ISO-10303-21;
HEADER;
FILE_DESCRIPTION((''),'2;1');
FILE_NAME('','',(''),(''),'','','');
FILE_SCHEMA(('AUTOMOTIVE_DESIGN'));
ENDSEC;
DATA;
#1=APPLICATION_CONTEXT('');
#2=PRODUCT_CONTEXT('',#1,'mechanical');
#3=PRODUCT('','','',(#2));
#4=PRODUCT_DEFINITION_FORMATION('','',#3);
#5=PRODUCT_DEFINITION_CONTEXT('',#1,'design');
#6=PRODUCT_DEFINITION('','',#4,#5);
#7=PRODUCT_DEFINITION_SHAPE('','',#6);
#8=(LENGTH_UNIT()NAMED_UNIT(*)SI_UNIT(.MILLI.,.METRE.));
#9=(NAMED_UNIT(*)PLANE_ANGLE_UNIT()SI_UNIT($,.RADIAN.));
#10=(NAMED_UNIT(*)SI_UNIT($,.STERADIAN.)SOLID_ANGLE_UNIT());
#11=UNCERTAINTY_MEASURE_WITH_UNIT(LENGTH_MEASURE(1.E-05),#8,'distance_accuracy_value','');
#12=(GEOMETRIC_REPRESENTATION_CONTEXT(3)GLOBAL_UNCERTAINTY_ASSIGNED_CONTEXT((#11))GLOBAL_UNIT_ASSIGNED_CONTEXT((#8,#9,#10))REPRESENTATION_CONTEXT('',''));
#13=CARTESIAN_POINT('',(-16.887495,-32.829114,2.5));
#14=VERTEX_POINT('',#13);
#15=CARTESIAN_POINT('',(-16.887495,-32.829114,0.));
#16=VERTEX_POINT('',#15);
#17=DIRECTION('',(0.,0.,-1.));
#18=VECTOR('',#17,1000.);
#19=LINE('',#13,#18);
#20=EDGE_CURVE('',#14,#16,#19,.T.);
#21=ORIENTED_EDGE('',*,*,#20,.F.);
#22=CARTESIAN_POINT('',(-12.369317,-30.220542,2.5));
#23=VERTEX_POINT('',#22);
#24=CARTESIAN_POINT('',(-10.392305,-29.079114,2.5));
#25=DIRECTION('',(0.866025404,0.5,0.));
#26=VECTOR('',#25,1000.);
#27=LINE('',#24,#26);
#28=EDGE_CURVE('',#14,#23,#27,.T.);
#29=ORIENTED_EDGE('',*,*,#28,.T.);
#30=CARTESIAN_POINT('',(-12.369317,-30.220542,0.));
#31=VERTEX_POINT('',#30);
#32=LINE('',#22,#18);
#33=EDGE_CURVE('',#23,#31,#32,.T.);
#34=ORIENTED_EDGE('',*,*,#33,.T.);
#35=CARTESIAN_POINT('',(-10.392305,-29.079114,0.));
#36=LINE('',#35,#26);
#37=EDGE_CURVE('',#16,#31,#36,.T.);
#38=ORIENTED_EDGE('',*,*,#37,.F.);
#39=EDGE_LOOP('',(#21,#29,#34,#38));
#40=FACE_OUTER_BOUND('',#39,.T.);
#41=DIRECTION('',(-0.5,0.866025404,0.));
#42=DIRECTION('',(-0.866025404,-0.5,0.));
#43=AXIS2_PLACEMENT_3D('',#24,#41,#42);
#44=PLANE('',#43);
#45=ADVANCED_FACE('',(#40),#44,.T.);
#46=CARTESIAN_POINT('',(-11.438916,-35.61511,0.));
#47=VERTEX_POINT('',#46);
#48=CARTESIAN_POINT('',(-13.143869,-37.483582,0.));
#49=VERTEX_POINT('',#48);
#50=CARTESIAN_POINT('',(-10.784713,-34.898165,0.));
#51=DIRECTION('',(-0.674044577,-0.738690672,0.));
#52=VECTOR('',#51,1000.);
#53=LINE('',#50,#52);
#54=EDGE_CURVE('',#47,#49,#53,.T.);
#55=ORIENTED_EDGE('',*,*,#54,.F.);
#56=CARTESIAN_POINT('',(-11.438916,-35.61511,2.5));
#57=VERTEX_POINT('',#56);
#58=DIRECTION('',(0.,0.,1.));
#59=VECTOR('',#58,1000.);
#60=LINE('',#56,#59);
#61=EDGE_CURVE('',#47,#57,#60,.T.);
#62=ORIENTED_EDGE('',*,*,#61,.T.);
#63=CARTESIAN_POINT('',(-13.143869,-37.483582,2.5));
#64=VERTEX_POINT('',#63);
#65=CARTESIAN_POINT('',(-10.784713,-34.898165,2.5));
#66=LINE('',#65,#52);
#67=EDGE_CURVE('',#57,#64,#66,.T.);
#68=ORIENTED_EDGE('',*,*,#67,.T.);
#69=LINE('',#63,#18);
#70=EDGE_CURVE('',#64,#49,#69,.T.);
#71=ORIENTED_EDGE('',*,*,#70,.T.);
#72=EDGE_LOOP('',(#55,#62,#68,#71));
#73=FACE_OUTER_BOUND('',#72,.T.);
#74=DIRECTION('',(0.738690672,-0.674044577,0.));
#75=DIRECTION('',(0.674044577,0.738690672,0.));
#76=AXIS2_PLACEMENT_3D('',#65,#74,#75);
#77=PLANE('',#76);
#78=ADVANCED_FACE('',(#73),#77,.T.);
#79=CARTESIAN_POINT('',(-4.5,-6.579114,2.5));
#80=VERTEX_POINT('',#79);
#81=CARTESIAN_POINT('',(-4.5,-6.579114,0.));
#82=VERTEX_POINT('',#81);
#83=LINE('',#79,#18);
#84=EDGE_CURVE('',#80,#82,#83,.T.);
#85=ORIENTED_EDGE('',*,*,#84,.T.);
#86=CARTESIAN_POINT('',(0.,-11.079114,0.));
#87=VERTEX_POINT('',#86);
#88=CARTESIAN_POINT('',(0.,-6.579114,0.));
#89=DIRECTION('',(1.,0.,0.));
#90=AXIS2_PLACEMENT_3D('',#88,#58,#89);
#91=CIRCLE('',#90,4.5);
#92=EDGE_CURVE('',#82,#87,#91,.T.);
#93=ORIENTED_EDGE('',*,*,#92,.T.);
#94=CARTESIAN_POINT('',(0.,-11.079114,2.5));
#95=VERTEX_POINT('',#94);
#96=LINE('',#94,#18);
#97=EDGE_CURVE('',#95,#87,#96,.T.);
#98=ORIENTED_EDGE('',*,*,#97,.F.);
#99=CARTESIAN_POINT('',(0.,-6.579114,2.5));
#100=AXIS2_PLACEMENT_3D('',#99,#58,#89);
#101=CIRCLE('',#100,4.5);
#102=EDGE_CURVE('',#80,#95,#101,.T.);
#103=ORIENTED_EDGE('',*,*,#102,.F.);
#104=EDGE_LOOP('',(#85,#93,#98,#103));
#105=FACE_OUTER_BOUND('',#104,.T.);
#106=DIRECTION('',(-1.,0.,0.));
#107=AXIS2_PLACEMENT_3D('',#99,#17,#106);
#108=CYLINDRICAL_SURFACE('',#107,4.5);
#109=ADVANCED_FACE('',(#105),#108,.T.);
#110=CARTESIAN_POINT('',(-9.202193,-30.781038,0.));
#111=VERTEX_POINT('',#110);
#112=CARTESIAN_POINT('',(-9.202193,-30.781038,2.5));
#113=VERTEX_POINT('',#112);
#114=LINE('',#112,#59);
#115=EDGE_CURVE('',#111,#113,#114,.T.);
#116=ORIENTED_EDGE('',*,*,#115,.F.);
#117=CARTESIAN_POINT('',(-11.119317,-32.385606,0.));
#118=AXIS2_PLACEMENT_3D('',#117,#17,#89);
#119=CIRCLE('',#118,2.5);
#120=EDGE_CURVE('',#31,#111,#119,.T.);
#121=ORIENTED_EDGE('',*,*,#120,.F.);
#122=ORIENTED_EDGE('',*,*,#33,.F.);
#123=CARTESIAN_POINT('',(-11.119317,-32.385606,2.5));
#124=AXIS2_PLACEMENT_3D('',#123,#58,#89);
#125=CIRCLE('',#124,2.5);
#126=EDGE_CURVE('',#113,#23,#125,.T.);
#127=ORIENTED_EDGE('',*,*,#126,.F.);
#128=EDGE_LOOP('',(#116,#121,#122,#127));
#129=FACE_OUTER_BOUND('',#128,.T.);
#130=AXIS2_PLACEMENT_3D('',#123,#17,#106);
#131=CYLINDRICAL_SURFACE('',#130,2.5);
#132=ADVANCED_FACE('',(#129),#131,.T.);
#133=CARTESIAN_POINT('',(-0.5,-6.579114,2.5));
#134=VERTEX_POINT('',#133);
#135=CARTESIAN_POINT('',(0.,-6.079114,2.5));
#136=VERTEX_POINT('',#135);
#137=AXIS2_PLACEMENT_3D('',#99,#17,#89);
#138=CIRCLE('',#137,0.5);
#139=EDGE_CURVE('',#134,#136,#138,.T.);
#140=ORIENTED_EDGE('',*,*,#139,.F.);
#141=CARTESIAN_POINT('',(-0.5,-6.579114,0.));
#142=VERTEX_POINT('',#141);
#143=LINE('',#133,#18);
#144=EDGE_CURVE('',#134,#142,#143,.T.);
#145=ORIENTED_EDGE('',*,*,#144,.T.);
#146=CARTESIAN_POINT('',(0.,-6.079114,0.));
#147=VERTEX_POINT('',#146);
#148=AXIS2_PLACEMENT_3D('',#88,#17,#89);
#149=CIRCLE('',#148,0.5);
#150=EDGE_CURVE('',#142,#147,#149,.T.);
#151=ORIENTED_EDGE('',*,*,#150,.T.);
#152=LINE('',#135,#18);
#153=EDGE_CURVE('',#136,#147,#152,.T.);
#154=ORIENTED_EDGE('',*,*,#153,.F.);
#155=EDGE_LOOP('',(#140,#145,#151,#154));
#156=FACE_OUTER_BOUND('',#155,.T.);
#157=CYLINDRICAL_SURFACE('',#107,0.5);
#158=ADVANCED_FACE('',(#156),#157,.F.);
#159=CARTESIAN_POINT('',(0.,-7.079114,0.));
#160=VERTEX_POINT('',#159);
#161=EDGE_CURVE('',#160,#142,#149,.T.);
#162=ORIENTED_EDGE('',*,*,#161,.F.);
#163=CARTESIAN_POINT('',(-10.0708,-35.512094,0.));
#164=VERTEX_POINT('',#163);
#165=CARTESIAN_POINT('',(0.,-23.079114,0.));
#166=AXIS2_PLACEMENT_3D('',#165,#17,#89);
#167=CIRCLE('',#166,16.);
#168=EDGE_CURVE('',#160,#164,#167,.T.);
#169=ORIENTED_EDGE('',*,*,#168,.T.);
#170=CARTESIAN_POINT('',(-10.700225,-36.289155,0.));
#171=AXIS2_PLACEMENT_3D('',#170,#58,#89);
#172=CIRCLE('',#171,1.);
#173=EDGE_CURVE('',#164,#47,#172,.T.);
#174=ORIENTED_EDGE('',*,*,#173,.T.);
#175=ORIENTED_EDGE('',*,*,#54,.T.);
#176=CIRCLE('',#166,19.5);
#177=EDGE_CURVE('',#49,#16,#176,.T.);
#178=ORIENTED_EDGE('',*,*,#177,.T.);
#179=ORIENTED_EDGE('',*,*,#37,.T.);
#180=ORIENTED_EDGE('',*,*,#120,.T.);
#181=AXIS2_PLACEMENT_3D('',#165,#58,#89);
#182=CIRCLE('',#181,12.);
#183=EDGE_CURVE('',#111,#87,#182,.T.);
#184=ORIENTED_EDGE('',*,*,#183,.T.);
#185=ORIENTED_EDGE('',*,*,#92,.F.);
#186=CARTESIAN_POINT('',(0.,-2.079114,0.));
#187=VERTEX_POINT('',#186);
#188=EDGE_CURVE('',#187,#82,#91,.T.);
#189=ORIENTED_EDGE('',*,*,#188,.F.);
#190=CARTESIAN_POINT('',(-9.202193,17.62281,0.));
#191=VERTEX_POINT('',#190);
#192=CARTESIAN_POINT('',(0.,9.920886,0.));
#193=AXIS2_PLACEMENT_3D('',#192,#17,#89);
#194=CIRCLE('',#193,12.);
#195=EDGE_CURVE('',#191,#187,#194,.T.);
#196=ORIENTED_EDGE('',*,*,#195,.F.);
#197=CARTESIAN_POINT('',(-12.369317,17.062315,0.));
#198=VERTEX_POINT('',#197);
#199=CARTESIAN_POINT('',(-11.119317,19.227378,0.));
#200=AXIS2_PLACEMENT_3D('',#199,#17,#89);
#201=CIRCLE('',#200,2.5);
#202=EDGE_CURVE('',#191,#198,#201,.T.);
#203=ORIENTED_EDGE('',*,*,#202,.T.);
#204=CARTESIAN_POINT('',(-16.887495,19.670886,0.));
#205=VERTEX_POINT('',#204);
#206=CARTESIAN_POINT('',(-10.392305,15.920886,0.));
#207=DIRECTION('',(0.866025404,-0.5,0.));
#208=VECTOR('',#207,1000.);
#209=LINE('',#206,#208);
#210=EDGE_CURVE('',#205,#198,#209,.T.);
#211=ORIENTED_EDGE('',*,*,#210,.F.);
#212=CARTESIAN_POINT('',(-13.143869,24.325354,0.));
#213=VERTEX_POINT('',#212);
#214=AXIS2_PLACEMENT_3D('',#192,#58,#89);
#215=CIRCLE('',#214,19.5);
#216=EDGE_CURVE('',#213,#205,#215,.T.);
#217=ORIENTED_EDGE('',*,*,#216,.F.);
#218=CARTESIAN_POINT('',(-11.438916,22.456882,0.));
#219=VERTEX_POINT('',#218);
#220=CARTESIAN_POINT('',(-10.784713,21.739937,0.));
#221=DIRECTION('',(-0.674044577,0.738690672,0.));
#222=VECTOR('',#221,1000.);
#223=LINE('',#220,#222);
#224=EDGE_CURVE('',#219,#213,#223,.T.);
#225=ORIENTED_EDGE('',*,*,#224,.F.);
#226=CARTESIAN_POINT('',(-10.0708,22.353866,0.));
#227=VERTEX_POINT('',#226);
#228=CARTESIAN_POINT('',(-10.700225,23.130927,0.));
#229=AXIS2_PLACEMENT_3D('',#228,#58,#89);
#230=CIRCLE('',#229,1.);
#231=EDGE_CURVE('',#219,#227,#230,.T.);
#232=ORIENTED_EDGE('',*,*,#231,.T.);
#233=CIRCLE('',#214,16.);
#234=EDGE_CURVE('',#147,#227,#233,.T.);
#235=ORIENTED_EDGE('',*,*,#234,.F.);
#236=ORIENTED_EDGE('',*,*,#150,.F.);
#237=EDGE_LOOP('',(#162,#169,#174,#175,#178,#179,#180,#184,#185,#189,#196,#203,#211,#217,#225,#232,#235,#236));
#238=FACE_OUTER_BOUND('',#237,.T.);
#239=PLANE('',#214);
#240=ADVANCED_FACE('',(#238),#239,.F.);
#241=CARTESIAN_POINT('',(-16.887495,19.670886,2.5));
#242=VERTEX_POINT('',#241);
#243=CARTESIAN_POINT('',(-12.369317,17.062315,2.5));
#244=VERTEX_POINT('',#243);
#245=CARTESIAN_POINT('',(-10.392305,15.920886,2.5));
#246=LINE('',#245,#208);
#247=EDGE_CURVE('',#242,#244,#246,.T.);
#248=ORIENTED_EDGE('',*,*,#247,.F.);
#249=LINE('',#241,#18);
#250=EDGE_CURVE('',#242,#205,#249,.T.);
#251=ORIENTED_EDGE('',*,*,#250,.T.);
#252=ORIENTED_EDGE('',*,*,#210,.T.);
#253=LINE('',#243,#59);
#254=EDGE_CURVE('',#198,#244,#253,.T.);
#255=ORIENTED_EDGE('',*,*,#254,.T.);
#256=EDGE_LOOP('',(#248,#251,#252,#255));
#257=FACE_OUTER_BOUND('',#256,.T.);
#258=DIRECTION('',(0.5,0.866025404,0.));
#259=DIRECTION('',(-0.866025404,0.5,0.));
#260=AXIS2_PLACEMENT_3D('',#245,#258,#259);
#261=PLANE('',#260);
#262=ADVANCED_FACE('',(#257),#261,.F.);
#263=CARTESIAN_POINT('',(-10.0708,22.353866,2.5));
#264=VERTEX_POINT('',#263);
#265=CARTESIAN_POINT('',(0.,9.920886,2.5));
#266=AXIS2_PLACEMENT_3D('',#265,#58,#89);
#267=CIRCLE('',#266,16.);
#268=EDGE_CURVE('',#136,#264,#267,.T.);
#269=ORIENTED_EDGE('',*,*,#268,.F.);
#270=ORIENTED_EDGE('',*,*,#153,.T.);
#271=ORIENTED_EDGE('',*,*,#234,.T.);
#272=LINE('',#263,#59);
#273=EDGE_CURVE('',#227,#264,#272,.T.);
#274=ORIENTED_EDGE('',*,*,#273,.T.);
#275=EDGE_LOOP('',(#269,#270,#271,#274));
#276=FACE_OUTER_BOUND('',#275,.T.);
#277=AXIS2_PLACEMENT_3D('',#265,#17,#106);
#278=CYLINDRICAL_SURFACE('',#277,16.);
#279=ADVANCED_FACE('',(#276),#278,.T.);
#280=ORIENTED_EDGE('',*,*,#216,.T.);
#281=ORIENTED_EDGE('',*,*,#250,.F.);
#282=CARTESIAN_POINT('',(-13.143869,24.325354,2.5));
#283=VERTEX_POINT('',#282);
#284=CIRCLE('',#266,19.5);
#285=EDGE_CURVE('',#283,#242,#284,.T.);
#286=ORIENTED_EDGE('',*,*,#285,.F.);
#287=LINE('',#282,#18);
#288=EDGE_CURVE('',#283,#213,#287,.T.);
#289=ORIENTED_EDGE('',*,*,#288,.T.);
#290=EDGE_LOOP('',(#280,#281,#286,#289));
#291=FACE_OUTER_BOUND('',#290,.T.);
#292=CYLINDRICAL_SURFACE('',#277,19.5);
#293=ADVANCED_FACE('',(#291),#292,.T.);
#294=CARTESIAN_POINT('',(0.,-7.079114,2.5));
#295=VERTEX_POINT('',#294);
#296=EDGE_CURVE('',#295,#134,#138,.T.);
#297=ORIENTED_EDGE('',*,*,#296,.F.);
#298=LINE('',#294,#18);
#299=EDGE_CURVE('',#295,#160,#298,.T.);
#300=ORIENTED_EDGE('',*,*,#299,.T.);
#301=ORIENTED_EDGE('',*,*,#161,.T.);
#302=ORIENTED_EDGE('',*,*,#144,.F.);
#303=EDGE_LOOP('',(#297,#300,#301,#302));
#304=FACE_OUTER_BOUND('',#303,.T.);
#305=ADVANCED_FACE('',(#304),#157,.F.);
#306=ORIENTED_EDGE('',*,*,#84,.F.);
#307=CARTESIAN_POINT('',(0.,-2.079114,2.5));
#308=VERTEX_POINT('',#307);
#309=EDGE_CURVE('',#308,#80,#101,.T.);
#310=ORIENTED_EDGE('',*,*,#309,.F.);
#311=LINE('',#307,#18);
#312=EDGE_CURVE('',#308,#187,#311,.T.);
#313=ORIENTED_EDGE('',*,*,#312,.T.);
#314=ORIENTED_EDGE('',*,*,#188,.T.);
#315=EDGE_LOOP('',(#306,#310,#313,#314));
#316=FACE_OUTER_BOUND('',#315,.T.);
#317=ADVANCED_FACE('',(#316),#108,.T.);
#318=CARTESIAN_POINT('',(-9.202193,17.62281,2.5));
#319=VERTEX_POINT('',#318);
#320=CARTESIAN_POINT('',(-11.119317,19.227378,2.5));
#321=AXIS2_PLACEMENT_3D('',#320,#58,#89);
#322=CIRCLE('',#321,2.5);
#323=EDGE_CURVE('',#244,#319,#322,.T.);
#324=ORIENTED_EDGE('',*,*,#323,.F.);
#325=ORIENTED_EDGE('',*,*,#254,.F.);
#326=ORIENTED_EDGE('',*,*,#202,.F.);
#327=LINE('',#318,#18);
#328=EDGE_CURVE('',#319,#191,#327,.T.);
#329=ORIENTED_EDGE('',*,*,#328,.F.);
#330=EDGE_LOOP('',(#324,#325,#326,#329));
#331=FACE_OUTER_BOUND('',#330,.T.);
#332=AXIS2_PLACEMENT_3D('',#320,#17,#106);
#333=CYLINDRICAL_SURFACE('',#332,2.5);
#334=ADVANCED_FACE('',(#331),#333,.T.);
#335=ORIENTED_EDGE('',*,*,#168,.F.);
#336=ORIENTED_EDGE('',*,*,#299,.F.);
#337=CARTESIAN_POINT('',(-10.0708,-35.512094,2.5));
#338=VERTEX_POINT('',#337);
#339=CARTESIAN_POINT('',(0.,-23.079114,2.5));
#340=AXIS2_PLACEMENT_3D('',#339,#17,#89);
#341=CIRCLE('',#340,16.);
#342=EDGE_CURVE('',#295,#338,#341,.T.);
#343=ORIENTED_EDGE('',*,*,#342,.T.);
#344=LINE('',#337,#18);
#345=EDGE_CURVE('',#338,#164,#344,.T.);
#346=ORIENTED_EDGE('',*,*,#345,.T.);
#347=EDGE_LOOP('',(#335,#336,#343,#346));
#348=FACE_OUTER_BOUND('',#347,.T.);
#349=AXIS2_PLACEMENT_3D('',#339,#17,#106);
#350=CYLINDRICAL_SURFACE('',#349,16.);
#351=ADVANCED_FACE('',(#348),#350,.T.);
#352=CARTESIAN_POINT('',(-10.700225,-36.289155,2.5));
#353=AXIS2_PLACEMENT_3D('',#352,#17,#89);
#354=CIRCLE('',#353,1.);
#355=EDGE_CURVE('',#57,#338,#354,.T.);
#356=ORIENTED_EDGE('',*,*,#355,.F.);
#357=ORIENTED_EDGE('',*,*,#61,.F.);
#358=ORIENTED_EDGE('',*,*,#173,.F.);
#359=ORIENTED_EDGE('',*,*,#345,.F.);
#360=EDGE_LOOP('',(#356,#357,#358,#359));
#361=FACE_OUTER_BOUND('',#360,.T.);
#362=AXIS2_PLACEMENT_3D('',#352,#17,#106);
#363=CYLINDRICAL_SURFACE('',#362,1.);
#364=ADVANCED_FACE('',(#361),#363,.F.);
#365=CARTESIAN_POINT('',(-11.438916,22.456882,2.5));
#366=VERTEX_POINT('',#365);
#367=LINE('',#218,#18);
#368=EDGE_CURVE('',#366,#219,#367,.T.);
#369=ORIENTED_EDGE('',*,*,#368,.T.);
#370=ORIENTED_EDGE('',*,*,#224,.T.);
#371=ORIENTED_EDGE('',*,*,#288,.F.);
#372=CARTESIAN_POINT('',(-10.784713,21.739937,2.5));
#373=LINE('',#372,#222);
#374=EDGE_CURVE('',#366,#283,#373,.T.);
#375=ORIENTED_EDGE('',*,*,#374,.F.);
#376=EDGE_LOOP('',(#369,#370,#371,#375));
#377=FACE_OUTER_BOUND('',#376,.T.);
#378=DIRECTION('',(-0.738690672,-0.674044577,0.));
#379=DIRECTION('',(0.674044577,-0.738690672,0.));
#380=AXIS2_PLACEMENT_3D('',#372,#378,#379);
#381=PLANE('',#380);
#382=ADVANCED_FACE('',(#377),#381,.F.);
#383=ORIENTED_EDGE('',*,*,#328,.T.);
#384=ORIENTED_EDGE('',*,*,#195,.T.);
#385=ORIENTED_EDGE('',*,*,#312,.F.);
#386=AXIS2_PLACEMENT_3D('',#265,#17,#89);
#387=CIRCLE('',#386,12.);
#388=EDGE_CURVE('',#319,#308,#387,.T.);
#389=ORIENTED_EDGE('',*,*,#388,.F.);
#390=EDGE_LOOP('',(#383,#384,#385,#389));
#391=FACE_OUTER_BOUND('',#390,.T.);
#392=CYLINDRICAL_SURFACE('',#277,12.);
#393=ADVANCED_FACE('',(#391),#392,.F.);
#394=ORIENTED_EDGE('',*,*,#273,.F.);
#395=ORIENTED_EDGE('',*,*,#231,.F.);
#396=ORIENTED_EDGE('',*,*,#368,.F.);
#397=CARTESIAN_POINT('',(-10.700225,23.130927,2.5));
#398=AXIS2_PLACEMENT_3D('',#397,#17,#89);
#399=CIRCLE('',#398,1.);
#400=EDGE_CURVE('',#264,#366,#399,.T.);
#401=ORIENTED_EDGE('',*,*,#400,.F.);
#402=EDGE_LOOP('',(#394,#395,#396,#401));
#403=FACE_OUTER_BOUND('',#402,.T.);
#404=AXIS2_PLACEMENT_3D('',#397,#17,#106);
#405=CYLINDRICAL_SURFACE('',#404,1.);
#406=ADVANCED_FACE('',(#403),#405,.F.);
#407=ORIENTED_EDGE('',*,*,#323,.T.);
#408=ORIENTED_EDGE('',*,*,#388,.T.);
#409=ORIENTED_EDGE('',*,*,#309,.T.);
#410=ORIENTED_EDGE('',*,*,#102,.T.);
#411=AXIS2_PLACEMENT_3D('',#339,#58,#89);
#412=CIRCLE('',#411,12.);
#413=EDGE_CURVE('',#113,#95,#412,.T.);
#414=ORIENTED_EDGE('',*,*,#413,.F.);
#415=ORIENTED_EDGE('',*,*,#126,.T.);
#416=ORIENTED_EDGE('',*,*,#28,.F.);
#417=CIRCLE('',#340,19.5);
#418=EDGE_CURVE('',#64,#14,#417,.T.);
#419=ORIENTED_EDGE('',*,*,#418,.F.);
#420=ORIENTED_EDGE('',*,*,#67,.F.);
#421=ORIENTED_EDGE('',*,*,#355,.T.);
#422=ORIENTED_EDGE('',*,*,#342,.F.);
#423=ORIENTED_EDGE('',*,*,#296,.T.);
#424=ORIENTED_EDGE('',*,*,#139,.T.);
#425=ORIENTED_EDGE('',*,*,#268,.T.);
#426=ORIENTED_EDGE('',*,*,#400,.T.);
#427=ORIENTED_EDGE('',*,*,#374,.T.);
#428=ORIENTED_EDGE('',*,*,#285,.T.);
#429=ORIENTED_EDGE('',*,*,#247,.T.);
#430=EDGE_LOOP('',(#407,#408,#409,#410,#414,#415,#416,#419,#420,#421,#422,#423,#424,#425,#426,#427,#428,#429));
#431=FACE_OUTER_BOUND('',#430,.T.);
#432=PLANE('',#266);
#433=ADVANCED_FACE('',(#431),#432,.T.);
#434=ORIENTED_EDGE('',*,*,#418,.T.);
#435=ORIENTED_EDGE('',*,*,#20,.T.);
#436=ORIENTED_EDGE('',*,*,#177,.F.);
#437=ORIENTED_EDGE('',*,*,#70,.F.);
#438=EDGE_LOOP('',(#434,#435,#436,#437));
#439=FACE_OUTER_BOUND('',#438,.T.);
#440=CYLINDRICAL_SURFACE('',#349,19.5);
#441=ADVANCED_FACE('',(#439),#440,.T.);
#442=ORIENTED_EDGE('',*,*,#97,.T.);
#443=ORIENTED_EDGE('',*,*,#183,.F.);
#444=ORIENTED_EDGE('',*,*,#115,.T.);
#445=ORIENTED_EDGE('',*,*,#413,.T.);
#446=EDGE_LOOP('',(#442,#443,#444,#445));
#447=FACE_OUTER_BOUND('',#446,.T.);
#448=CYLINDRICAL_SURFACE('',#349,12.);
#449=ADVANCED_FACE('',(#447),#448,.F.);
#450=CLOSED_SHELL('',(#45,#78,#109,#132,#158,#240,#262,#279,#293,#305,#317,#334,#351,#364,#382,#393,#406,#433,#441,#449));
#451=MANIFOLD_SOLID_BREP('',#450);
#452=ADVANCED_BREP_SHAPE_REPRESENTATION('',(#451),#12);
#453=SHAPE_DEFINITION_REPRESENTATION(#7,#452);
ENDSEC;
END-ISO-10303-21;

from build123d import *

# Parameters (mm, degrees)
EXTRUDE_1_DEPTH        = 2.5
FILLET_1_R             = 1
FILLET_2_R             = 2.5
FILLET_1_OF_MIRROR_1_R = 1
FILLET_2_OF_MIRROR_1_R = 2.5


with BuildPart() as part:
    # 草图2 → 凸台-拉伸1 (new body)
    with BuildSketch(Plane.XY):
        with BuildLine():
            Line((-4.5, -6.579113924), (-0.5, -6.579113924))
            ThreePointArc((-0.5, -6.579113924), (-0.353553391, -6.225560533), (0, -6.079113924))
            ThreePointArc((0, -6.079113924), (14.918190439, 15.70427557), (-10.784713231, 21.739936821))
            Line((-10.784713231, 21.739936821), (-13.143869251, 24.325354172))
            ThreePointArc((-13.143869251, 24.325354172), (-15.194957506, 22.142312604), (-16.887495374, 19.670886076))
            Line((-16.887495374, 19.670886076), (-10.392304845, 15.920886076))
            ThreePointArc((-10.392304845, 15.920886076), (10.392304845, 15.920886076), (0, -2.079113924))
            ThreePointArc((0, -2.079113924), (-3.181980515, -3.397133409), (-4.5, -6.579113924))
        make_face()
    extrude_1 = extrude(amount=EXTRUDE_1_DEPTH)

    # 圆角1
    fillet_1_edges = [part.edges().sort_by_distance(p)[0] for p in [
        (-10.784713231, 21.739936821, 1.25),
    ]]
    fillet(fillet_1_edges, radius=FILLET_1_R)

    # 圆角2
    fillet_2_edges = [part.edges().sort_by_distance(p)[0] for p in [
        (-10.392304845, 15.920886076, 1.25),
    ]]
    fillet(fillet_2_edges, radius=FILLET_2_R)

    # 镜向1: 凸台-拉伸1 across plane
    add(extrude_1.mirror(Plane.ZX.offset(-6.579113924)))

    # 圆角1 of 镜向1
    fillet_1_of_mirror_1_edges = [part.edges().sort_by_distance(p)[0] for p in [
        (-10.784713231, -34.898164669, 1.25),
    ]]
    fillet(fillet_1_of_mirror_1_edges, radius=FILLET_1_OF_MIRROR_1_R)

    # 圆角2 of 镜向1
    fillet_2_of_mirror_1_edges = [part.edges().sort_by_distance(p)[0] for p in [
        (-10.392304845, -29.079113924, 1.25),
    ]]
    fillet(fillet_2_of_mirror_1_edges, radius=FILLET_2_OF_MIRROR_1_R)


solid = part.part
